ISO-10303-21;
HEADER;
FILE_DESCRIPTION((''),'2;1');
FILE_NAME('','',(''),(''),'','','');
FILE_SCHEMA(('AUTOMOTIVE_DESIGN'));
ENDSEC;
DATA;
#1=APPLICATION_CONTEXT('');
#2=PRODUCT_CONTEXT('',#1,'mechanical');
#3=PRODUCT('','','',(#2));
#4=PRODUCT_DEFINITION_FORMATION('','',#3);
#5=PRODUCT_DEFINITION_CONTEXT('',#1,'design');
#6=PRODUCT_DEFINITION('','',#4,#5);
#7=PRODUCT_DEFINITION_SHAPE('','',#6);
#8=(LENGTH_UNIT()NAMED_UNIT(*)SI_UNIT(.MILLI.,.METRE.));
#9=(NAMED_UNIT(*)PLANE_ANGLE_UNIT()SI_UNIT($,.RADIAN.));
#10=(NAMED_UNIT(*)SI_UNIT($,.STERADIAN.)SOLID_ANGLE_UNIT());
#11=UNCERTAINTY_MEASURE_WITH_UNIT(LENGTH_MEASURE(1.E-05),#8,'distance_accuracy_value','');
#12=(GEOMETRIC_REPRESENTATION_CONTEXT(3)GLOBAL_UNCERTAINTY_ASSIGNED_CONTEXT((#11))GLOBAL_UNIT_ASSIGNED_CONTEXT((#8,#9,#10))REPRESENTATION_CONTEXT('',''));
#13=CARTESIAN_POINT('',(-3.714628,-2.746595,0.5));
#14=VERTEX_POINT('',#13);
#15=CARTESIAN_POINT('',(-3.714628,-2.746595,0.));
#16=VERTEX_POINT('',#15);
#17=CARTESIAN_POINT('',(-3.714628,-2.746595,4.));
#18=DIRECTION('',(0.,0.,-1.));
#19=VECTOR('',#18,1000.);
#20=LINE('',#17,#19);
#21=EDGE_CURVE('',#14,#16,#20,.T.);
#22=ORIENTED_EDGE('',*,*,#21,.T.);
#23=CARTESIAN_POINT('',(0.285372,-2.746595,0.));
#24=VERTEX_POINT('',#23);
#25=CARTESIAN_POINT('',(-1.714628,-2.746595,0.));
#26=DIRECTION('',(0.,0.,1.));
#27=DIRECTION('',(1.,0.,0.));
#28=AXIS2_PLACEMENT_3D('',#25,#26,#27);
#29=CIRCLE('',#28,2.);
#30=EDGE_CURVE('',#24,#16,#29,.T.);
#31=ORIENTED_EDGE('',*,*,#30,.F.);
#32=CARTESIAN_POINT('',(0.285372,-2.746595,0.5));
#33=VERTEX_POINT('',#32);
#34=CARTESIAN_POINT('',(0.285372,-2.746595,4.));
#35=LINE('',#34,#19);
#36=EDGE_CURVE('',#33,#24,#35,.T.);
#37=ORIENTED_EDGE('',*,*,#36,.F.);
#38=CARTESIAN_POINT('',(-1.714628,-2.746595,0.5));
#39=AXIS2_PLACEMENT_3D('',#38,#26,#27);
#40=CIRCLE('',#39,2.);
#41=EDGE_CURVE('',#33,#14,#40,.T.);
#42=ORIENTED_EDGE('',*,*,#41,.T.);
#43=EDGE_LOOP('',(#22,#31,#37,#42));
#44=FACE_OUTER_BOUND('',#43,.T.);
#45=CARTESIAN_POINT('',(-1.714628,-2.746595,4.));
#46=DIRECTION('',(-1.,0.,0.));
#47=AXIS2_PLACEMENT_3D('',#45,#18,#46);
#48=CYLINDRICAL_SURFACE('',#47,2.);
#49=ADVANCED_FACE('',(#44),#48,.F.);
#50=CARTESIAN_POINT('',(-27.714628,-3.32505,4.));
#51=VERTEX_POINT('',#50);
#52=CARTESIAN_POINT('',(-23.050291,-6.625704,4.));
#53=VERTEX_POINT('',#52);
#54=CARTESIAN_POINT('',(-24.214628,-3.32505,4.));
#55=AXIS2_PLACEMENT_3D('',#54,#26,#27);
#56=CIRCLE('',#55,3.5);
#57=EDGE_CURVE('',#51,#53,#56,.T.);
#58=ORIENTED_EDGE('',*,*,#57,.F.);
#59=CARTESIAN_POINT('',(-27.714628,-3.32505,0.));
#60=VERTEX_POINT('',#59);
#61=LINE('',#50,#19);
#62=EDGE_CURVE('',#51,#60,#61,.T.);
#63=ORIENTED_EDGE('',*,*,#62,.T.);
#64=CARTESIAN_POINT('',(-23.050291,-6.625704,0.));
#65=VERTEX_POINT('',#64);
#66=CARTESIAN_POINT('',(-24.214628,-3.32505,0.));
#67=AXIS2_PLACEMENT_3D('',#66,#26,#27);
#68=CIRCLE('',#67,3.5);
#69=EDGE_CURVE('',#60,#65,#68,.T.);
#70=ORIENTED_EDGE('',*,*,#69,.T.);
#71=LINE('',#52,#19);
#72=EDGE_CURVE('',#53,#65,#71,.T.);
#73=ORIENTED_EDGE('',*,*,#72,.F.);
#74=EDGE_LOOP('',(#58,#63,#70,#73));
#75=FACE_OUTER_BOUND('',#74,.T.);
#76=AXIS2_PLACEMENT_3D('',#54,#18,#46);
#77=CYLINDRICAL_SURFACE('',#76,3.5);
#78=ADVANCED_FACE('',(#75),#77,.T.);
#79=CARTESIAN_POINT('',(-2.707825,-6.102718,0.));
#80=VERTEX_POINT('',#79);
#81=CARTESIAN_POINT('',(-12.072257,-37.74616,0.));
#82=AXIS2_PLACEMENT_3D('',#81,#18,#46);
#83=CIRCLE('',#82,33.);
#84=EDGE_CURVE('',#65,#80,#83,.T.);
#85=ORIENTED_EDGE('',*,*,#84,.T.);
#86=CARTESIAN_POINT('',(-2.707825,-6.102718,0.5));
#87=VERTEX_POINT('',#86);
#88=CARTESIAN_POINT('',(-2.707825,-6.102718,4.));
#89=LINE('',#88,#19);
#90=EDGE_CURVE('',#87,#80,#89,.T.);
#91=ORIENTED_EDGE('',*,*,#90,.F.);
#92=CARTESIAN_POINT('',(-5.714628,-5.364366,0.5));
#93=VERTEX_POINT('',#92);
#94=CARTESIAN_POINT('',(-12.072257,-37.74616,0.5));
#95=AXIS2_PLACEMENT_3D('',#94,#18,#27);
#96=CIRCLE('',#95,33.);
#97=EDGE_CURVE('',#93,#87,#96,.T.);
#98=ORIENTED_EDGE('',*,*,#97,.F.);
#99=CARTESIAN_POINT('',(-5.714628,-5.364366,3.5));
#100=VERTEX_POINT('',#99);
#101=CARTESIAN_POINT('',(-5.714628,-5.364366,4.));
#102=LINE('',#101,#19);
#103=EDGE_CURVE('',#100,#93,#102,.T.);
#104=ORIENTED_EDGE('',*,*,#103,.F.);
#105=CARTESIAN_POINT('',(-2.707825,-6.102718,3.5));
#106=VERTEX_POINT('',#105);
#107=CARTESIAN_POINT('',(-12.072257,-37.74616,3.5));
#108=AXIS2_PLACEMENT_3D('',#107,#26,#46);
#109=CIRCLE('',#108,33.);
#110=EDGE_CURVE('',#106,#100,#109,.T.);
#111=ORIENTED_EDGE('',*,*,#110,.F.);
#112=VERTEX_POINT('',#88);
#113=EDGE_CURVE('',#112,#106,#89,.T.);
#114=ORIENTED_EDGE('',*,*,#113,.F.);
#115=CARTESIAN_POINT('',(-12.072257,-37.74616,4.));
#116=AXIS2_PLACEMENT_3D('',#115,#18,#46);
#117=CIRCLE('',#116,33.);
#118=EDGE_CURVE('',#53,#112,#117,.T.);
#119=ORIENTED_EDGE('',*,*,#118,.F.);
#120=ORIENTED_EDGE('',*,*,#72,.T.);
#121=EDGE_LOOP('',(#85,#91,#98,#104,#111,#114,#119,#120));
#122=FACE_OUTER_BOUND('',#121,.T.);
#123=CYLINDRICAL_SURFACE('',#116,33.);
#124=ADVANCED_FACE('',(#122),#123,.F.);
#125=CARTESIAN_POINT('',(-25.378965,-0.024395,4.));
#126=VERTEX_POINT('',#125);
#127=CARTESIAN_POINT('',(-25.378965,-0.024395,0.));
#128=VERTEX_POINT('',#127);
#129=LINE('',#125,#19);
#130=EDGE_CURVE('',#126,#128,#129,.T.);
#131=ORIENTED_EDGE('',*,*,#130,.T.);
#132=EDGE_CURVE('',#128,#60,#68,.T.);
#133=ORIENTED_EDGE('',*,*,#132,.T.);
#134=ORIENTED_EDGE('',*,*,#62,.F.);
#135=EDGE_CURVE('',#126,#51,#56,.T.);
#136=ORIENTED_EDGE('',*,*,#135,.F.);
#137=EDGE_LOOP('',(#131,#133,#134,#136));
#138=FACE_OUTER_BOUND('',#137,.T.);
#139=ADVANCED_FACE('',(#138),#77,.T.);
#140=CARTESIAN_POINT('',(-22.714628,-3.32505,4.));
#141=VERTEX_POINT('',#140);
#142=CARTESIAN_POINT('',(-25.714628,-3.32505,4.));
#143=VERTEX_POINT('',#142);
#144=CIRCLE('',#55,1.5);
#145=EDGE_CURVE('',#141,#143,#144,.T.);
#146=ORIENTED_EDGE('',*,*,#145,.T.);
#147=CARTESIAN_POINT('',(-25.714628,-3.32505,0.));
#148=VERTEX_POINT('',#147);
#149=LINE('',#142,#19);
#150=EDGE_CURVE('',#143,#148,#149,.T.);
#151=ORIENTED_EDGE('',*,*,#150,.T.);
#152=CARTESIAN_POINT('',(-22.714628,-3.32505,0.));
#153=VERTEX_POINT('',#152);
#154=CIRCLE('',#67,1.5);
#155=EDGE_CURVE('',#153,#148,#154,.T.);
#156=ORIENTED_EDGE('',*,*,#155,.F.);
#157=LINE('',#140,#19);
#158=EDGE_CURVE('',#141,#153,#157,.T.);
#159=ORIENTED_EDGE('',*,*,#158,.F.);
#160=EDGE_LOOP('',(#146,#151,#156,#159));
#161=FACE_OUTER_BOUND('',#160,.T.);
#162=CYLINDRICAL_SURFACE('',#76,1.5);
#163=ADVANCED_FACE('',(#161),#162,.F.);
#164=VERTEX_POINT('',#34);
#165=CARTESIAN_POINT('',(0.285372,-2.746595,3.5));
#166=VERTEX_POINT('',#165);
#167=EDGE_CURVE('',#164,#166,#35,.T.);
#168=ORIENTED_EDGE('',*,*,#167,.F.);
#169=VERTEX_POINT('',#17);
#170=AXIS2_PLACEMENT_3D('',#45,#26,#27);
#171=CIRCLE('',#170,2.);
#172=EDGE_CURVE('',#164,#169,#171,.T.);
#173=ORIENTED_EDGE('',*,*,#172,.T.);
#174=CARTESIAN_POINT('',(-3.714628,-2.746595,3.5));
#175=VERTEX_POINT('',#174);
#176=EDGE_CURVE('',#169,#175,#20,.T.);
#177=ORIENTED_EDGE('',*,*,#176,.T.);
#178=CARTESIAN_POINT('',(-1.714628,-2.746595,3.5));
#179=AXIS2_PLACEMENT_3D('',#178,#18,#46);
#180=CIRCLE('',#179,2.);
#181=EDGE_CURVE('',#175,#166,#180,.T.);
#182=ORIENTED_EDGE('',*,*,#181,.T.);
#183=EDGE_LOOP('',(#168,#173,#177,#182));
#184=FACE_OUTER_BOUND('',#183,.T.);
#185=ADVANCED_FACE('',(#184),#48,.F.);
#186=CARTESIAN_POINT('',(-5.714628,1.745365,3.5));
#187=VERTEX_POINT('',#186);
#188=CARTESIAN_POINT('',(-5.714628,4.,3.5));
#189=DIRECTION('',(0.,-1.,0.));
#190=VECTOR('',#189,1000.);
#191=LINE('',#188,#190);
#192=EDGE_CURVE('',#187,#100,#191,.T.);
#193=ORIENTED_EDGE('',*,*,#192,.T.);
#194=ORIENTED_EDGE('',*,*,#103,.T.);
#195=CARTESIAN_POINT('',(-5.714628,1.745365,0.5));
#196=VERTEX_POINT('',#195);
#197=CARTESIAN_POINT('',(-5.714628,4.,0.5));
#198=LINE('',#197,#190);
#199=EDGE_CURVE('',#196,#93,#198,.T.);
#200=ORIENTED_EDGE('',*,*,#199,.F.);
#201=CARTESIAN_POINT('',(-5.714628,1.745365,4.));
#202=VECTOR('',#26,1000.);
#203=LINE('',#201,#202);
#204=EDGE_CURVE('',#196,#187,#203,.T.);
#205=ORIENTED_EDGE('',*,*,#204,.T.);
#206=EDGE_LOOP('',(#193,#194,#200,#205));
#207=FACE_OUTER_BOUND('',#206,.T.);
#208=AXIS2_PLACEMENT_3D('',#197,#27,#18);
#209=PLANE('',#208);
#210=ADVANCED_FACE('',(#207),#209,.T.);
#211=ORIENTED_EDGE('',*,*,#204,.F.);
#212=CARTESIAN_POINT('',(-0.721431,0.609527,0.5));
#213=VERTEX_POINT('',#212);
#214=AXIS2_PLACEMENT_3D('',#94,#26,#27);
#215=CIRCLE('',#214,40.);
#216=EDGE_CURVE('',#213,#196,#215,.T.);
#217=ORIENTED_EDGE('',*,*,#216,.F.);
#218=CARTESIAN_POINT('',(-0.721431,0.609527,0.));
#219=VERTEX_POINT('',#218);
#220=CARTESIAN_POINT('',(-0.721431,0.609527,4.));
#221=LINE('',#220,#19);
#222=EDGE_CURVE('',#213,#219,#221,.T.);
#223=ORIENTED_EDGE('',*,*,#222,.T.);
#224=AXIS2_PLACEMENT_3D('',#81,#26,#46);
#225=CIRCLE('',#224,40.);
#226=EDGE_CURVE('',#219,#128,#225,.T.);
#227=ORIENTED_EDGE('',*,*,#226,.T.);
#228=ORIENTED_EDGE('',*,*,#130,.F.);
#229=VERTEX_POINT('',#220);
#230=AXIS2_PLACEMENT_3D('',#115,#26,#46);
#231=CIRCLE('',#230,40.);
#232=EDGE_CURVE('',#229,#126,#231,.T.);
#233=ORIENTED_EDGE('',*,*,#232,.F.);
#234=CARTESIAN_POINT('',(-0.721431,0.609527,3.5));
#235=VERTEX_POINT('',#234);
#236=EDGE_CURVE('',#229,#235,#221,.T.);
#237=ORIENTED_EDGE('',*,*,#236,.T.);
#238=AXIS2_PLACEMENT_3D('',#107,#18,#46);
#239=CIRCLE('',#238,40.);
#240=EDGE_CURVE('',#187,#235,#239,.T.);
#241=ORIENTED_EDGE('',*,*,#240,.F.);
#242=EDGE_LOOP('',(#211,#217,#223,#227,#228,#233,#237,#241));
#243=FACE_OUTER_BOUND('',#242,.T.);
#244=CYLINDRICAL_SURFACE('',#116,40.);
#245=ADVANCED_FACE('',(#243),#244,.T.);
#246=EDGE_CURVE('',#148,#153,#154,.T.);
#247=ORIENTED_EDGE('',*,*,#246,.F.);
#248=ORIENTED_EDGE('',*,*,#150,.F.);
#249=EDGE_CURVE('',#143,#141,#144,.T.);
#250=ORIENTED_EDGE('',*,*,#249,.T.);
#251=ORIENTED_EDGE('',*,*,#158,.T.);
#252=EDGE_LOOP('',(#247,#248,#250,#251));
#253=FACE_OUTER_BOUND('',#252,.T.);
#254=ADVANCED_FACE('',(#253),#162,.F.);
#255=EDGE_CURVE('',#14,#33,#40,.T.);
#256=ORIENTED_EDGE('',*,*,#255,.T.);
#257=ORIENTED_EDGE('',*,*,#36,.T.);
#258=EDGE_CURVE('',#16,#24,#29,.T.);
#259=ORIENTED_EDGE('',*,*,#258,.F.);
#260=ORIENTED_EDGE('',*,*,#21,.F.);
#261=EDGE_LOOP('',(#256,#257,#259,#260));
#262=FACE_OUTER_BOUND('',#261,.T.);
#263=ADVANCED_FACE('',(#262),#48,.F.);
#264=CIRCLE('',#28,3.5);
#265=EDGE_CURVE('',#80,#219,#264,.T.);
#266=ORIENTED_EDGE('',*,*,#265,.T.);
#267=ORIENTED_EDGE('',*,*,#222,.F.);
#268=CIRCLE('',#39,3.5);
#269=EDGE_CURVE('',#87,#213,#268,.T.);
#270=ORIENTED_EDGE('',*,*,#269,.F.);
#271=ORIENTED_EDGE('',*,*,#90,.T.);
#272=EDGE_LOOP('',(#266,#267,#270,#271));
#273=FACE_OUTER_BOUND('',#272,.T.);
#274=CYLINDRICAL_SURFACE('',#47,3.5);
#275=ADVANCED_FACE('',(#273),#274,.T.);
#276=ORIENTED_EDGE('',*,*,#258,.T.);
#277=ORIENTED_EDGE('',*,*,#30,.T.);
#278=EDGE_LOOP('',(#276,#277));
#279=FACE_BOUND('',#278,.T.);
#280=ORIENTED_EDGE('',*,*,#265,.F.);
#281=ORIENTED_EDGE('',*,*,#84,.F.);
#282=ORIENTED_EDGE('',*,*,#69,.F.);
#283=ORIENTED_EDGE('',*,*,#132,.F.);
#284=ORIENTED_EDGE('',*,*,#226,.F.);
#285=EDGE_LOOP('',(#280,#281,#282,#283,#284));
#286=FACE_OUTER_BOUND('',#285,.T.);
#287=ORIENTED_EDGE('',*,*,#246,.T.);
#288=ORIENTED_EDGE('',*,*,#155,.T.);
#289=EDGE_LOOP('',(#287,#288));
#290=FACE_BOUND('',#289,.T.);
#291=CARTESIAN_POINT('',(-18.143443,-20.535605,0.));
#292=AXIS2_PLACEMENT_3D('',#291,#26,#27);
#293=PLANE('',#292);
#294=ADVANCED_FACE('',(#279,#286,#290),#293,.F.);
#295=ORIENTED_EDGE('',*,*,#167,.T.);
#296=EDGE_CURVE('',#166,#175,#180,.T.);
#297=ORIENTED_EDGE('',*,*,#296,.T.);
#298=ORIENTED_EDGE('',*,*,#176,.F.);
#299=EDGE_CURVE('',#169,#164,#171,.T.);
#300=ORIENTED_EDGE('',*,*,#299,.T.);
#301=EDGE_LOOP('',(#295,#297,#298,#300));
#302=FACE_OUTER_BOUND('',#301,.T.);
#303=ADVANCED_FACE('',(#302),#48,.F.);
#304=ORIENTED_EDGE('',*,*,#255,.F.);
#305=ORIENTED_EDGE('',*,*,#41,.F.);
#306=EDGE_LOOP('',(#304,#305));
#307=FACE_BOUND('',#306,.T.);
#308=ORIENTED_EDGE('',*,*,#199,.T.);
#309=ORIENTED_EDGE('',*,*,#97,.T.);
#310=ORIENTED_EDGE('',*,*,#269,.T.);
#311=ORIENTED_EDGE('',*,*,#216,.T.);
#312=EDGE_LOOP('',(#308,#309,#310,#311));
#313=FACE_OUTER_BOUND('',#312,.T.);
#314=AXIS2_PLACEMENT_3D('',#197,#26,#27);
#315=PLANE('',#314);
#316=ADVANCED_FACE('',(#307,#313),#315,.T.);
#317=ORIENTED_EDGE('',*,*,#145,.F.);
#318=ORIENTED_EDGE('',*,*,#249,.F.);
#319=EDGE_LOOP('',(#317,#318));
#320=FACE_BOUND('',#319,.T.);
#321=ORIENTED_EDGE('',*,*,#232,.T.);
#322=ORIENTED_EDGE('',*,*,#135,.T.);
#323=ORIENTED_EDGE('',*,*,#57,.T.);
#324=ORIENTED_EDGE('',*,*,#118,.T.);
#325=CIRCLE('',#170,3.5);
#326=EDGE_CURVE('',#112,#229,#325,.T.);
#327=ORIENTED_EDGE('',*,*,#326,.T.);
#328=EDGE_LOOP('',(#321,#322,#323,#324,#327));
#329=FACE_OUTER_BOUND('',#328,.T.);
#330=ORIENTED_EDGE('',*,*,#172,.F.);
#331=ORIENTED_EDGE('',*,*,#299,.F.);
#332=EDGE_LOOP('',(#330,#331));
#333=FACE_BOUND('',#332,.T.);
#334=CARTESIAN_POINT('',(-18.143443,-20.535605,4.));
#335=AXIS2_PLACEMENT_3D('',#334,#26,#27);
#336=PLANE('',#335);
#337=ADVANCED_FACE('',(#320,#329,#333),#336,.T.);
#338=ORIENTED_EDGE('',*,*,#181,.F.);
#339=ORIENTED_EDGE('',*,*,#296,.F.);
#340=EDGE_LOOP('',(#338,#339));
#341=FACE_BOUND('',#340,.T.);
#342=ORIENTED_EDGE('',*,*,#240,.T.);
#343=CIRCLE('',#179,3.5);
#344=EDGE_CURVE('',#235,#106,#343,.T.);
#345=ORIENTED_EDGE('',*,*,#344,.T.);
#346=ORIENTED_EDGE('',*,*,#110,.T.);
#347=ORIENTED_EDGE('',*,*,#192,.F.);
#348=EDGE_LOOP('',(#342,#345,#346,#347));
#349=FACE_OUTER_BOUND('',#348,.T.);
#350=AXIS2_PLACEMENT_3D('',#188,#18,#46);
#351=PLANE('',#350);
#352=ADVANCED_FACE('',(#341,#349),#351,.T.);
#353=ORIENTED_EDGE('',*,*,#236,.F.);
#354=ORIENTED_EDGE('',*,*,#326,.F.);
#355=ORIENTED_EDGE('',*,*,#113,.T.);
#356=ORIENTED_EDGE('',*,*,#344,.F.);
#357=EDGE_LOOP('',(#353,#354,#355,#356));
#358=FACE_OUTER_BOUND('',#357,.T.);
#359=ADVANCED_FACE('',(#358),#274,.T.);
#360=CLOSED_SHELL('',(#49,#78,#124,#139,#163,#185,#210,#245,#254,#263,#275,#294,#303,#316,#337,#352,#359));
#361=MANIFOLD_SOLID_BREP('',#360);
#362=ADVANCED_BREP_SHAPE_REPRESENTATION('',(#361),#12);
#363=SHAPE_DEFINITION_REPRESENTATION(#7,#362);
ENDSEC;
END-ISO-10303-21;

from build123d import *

# Parameters (mm, degrees)
SKETCH1_R               = 3
SKETCH1_R_2             = 4
BOSS_EXTRUDE1_DEPTH     = 8
CUT_EXTRUDE1_DEPTH      = 8
CUT_EXTRUDE1_DEPTH_BACK = 16
SKETCH2_W               = 30
SKETCH2_H               = 6
SCALE1_SCALE            = 0.5


with BuildPart() as part:
    # Sketch1 → Boss-Extrude1 (new body)
    with BuildSketch(Plane.XY):
        with BuildLine():
            ThreePointArc((-50.757929877, -0.048790598), (-26.200561377, 4.481254982), (-1.442861384, 1.219054549))
            ThreePointArc((-1.442861384, 1.219054549), (3.282989256, -7.479585329), (-5.415650622, -12.205435969))
            ThreePointArc((-5.415650622, -12.205435969), (-25.840753116, -9.514120612), (-46.100582129, -13.251408215))
            ThreePointArc((-46.100582129, -13.251408215), (-55.030564812, -8.978773281), (-50.757929877, -0.048790598))
        make_face()
        with Locations((-48.429256003, -6.650099407)):
            Circle(SKETCH1_R, mode=Mode.SUBTRACT)
        with Locations((-3.429256003, -5.49319071)):
            Circle(SKETCH1_R_2, mode=Mode.SUBTRACT)
    extrude(amount=BOSS_EXTRUDE1_DEPTH)

    # Sketch2 → Cut-Extrude1 (cut, two sides: drawn at the far end of the back side and taken through both)
    with BuildSketch(Plane(origin=(0, 0, 0), x_dir=(1, 0, 0), z_dir=(0, 1, 0)).offset(-CUT_EXTRUDE1_DEPTH_BACK)):
        with Locations((3.570743997, -4)):
            Rectangle(SKETCH2_W, SKETCH2_H)
    extrude(amount=CUT_EXTRUDE1_DEPTH + CUT_EXTRUDE1_DEPTH_BACK, mode=Mode.SUBTRACT)


with BuildPart() as part_1:
    # Scale1: scaled about (0, 0, 0)
    add(part.part.scale(SCALE1_SCALE))


solid = part_1.part
